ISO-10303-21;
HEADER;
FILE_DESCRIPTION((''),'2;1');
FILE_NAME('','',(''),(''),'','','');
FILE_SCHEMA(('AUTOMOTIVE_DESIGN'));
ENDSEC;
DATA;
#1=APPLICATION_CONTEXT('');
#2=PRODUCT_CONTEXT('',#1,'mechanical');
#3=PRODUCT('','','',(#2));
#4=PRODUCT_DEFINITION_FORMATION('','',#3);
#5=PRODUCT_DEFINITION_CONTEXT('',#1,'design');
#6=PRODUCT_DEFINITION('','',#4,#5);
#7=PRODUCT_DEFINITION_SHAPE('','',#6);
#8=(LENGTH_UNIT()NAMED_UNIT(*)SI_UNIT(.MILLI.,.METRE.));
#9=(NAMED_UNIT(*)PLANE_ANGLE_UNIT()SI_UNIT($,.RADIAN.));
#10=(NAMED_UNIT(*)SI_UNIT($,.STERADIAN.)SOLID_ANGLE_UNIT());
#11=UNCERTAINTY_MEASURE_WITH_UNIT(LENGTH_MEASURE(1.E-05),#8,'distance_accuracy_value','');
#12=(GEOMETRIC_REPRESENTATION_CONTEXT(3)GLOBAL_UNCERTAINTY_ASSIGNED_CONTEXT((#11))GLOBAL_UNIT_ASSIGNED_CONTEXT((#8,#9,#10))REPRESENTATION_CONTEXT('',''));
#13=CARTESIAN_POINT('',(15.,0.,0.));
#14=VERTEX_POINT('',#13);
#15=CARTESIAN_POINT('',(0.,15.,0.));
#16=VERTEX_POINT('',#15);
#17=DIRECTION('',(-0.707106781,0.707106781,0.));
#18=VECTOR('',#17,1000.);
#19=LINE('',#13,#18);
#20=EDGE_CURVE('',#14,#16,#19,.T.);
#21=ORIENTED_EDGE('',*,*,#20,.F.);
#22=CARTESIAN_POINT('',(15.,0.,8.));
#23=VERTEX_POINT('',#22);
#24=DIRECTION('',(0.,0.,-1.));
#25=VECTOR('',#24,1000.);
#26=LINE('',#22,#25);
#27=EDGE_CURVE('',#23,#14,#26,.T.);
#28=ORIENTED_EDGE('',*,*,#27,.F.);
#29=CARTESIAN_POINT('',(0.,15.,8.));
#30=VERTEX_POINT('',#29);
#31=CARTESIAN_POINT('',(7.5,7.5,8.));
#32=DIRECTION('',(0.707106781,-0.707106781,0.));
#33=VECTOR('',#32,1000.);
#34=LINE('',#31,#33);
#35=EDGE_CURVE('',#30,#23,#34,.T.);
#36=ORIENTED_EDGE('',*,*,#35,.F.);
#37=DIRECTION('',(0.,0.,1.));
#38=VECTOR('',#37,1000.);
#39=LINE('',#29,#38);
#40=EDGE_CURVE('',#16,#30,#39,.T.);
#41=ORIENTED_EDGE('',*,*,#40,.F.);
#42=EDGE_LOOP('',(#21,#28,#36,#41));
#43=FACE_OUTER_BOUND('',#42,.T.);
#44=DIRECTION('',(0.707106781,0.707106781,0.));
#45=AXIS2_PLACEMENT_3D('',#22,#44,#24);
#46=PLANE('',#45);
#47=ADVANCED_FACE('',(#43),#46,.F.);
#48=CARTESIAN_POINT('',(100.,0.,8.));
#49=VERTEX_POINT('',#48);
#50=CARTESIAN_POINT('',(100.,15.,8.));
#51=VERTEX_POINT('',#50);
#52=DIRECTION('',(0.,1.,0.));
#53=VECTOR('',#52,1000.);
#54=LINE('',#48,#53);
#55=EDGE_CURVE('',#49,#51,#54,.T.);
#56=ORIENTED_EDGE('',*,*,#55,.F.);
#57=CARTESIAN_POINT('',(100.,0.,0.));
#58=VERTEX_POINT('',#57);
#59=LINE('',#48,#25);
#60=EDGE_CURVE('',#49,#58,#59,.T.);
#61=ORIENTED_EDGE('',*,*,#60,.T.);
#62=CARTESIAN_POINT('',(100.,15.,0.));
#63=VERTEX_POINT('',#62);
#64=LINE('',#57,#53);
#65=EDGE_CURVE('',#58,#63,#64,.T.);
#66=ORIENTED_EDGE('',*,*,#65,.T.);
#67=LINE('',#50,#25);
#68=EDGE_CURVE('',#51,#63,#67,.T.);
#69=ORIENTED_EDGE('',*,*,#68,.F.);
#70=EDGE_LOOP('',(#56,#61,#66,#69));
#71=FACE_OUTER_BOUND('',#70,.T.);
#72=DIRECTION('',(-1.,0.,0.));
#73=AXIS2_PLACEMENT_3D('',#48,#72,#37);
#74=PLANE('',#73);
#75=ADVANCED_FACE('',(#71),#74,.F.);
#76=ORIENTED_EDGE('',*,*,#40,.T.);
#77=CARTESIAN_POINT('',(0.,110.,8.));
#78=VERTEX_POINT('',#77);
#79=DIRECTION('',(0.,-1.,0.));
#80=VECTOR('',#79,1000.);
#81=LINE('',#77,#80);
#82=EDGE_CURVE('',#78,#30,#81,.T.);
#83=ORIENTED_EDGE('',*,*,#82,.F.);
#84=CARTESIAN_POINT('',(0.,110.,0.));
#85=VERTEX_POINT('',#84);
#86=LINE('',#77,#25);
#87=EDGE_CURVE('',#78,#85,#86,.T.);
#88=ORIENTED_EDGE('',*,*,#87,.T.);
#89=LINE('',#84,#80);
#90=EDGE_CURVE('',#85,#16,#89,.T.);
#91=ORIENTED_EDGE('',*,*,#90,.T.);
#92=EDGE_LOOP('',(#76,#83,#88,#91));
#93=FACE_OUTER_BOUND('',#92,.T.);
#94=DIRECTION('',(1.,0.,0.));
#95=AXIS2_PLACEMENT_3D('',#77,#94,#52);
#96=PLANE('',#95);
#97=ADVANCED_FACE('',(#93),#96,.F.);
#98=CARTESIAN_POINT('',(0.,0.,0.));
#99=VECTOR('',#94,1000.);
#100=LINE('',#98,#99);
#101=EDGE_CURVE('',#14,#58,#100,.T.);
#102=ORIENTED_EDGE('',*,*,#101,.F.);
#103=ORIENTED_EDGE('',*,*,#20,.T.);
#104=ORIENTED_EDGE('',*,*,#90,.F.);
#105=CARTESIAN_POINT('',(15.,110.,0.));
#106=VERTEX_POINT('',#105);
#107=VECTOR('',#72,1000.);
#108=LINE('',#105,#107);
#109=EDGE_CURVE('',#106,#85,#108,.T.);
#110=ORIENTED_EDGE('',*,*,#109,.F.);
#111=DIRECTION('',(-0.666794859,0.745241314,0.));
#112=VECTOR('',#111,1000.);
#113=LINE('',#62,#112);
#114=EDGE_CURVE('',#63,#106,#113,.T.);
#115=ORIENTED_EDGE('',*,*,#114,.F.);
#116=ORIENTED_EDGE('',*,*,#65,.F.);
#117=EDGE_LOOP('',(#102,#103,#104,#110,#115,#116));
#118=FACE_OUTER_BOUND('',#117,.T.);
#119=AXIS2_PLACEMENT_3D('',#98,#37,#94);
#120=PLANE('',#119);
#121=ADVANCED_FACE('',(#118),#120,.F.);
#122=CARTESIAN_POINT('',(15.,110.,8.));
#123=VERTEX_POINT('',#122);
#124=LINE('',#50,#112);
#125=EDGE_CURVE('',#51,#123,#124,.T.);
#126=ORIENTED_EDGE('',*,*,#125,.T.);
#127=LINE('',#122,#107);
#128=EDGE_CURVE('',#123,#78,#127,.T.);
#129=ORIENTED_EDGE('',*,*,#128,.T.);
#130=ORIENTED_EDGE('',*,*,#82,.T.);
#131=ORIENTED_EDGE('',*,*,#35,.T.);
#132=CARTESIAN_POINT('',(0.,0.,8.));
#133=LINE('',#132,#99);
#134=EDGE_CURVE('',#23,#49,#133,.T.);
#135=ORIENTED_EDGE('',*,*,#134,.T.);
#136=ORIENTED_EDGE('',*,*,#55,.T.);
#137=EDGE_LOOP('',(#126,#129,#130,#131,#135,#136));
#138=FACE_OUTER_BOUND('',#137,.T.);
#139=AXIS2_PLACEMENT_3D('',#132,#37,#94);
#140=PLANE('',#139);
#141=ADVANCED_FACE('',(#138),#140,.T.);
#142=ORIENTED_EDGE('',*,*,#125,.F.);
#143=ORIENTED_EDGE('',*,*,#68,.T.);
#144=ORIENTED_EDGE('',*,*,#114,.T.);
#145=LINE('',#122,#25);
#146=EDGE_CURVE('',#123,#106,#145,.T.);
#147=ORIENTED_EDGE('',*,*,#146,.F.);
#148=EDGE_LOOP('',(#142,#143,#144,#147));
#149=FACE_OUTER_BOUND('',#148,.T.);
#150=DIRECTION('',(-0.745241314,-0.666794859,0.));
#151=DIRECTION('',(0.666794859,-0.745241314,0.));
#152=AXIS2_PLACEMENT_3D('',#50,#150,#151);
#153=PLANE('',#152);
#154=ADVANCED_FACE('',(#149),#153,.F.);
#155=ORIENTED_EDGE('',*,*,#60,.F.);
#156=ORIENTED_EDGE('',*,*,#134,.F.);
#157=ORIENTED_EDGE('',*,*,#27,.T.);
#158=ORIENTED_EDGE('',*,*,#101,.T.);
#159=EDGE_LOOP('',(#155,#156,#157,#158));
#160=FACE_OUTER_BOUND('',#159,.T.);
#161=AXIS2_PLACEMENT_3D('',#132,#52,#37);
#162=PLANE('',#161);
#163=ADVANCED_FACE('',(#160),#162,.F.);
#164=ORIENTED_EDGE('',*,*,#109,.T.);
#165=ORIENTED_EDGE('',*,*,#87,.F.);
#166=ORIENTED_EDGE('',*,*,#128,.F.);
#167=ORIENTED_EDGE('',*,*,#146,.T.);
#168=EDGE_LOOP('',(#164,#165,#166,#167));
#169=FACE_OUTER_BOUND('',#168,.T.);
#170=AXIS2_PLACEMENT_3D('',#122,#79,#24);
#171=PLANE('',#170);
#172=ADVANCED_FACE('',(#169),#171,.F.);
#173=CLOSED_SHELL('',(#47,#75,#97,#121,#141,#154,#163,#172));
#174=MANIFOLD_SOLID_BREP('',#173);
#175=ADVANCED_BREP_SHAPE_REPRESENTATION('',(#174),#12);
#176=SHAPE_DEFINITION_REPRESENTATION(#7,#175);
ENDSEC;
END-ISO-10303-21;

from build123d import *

# Parameters (mm, degrees)
EXTRUDE_1_DEPTH = 8
CHAMFER_1_SIZE  = 15


with BuildPart() as part:
    # 草图1 → 凸台-拉伸1 (new body)
    with BuildSketch(Plane.XY):
        Polygon((0, 0), (100, 0), (100, 15), (15, 110), (0, 110), align=None)
    extrude(amount=EXTRUDE_1_DEPTH)

    # 倒角1
    chamfer_1_edges = [part.edges().sort_by_distance(p)[0] for p in [
        (0, 0, 4),
    ]]
    chamfer(chamfer_1_edges, length=CHAMFER_1_SIZE)


solid = part.part
